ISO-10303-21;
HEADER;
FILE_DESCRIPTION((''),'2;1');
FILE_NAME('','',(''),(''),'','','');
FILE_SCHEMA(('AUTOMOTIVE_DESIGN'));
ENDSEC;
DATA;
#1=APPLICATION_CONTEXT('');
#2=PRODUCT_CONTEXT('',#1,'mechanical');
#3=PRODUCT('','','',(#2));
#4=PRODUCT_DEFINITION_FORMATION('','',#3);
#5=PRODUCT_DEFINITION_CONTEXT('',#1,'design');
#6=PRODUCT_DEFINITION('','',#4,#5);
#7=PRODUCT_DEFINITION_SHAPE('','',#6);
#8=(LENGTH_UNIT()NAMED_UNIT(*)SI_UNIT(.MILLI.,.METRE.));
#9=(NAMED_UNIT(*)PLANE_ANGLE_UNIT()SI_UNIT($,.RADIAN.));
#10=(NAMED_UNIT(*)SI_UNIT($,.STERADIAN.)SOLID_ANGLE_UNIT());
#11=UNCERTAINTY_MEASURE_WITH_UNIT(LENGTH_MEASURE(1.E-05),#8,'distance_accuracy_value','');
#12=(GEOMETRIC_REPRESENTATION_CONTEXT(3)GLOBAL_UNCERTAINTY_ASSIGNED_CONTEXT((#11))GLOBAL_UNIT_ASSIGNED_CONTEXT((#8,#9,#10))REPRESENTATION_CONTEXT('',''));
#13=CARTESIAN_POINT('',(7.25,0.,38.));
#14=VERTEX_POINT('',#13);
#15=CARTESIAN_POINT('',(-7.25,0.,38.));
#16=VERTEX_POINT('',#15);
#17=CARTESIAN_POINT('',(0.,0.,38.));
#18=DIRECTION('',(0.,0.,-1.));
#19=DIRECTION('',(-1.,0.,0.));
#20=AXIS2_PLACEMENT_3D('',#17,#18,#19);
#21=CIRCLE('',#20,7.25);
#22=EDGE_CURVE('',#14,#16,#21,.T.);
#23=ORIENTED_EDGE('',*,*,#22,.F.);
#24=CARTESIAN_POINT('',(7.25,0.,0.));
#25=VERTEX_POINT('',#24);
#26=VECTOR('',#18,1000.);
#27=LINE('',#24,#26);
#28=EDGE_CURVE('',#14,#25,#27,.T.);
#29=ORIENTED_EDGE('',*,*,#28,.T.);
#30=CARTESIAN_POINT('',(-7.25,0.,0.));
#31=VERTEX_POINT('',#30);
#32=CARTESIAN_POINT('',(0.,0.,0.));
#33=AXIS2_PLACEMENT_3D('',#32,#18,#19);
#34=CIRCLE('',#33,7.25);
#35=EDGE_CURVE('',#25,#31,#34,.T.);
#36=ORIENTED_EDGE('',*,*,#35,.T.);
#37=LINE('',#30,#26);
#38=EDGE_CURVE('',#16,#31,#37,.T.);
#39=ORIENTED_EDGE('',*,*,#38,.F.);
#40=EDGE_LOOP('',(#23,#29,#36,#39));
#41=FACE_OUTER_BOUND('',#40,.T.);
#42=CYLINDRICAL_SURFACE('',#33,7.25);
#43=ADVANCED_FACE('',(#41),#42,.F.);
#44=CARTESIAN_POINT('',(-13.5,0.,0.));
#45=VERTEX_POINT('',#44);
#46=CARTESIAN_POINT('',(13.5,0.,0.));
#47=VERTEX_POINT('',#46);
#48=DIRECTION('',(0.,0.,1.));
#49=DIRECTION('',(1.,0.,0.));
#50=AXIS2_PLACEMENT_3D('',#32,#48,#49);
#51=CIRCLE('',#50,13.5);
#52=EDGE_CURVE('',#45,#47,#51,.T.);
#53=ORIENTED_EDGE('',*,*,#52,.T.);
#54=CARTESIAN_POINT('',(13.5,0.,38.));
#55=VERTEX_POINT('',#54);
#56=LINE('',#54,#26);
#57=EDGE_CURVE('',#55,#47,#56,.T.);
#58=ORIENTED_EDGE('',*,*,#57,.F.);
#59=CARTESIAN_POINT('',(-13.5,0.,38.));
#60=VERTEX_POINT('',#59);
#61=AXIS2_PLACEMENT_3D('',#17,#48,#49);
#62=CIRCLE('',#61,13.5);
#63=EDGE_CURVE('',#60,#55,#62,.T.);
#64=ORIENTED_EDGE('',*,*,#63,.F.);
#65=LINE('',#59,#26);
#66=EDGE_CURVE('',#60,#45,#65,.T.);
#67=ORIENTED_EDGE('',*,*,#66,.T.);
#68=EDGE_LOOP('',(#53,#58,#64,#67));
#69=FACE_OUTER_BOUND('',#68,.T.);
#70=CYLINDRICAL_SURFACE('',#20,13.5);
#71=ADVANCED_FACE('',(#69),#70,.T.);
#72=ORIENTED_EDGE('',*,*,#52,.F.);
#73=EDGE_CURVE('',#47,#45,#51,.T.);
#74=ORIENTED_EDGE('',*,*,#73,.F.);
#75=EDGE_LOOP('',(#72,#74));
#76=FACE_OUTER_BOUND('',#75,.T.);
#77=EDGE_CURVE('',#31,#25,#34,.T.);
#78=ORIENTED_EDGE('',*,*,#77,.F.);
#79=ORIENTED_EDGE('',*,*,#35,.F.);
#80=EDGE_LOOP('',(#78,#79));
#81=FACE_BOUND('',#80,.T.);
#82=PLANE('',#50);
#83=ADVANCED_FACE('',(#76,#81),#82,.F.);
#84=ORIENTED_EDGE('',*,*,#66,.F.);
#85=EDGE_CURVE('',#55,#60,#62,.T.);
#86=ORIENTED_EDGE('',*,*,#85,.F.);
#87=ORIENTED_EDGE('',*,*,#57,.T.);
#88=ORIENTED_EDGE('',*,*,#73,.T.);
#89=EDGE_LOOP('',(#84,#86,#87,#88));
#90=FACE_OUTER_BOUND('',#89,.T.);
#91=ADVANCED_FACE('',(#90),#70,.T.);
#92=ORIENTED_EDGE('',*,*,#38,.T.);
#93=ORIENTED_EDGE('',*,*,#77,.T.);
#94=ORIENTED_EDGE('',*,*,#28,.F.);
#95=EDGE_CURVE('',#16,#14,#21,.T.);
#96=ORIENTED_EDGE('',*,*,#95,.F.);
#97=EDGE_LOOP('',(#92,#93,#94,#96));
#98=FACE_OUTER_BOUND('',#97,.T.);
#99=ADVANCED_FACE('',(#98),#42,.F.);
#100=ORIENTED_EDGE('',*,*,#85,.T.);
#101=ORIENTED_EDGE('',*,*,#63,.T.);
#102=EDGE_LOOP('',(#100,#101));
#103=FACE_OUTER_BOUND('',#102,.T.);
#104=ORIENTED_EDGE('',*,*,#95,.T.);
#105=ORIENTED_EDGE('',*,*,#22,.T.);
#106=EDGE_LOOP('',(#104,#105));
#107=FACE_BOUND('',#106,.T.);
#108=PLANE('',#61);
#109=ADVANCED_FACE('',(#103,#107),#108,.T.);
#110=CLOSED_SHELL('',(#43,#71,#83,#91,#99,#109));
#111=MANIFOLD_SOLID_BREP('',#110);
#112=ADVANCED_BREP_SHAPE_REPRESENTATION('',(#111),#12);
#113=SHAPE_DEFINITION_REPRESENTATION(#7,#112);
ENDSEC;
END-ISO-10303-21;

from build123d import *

# Parameters (mm, degrees)
SKETCH1_R              = 13.5
SKETCH1_R_2            = 6.5
BOSS_EXTRUDE1_DEPTH    = 38
M16X1_5_TAPPED_HOLE1_D = 14.5


with BuildPart() as part:
    # Sketch1 → Boss-Extrude1 (new body)
    with BuildSketch(Plane.XY):
        Circle(SKETCH1_R)
        Circle(SKETCH1_R_2, mode=Mode.SUBTRACT)
    extrude(amount=BOSS_EXTRUDE1_DEPTH)

    # M16x1.5 Tapped Hole1 (through all)
    with Locations(Plane(origin=(0, 0, 0), x_dir=(-1, 0, 0), z_dir=(0, 0, -1))):
        with Locations((0, 0)):
            Hole(M16X1_5_TAPPED_HOLE1_D / 2)


solid = part.part
